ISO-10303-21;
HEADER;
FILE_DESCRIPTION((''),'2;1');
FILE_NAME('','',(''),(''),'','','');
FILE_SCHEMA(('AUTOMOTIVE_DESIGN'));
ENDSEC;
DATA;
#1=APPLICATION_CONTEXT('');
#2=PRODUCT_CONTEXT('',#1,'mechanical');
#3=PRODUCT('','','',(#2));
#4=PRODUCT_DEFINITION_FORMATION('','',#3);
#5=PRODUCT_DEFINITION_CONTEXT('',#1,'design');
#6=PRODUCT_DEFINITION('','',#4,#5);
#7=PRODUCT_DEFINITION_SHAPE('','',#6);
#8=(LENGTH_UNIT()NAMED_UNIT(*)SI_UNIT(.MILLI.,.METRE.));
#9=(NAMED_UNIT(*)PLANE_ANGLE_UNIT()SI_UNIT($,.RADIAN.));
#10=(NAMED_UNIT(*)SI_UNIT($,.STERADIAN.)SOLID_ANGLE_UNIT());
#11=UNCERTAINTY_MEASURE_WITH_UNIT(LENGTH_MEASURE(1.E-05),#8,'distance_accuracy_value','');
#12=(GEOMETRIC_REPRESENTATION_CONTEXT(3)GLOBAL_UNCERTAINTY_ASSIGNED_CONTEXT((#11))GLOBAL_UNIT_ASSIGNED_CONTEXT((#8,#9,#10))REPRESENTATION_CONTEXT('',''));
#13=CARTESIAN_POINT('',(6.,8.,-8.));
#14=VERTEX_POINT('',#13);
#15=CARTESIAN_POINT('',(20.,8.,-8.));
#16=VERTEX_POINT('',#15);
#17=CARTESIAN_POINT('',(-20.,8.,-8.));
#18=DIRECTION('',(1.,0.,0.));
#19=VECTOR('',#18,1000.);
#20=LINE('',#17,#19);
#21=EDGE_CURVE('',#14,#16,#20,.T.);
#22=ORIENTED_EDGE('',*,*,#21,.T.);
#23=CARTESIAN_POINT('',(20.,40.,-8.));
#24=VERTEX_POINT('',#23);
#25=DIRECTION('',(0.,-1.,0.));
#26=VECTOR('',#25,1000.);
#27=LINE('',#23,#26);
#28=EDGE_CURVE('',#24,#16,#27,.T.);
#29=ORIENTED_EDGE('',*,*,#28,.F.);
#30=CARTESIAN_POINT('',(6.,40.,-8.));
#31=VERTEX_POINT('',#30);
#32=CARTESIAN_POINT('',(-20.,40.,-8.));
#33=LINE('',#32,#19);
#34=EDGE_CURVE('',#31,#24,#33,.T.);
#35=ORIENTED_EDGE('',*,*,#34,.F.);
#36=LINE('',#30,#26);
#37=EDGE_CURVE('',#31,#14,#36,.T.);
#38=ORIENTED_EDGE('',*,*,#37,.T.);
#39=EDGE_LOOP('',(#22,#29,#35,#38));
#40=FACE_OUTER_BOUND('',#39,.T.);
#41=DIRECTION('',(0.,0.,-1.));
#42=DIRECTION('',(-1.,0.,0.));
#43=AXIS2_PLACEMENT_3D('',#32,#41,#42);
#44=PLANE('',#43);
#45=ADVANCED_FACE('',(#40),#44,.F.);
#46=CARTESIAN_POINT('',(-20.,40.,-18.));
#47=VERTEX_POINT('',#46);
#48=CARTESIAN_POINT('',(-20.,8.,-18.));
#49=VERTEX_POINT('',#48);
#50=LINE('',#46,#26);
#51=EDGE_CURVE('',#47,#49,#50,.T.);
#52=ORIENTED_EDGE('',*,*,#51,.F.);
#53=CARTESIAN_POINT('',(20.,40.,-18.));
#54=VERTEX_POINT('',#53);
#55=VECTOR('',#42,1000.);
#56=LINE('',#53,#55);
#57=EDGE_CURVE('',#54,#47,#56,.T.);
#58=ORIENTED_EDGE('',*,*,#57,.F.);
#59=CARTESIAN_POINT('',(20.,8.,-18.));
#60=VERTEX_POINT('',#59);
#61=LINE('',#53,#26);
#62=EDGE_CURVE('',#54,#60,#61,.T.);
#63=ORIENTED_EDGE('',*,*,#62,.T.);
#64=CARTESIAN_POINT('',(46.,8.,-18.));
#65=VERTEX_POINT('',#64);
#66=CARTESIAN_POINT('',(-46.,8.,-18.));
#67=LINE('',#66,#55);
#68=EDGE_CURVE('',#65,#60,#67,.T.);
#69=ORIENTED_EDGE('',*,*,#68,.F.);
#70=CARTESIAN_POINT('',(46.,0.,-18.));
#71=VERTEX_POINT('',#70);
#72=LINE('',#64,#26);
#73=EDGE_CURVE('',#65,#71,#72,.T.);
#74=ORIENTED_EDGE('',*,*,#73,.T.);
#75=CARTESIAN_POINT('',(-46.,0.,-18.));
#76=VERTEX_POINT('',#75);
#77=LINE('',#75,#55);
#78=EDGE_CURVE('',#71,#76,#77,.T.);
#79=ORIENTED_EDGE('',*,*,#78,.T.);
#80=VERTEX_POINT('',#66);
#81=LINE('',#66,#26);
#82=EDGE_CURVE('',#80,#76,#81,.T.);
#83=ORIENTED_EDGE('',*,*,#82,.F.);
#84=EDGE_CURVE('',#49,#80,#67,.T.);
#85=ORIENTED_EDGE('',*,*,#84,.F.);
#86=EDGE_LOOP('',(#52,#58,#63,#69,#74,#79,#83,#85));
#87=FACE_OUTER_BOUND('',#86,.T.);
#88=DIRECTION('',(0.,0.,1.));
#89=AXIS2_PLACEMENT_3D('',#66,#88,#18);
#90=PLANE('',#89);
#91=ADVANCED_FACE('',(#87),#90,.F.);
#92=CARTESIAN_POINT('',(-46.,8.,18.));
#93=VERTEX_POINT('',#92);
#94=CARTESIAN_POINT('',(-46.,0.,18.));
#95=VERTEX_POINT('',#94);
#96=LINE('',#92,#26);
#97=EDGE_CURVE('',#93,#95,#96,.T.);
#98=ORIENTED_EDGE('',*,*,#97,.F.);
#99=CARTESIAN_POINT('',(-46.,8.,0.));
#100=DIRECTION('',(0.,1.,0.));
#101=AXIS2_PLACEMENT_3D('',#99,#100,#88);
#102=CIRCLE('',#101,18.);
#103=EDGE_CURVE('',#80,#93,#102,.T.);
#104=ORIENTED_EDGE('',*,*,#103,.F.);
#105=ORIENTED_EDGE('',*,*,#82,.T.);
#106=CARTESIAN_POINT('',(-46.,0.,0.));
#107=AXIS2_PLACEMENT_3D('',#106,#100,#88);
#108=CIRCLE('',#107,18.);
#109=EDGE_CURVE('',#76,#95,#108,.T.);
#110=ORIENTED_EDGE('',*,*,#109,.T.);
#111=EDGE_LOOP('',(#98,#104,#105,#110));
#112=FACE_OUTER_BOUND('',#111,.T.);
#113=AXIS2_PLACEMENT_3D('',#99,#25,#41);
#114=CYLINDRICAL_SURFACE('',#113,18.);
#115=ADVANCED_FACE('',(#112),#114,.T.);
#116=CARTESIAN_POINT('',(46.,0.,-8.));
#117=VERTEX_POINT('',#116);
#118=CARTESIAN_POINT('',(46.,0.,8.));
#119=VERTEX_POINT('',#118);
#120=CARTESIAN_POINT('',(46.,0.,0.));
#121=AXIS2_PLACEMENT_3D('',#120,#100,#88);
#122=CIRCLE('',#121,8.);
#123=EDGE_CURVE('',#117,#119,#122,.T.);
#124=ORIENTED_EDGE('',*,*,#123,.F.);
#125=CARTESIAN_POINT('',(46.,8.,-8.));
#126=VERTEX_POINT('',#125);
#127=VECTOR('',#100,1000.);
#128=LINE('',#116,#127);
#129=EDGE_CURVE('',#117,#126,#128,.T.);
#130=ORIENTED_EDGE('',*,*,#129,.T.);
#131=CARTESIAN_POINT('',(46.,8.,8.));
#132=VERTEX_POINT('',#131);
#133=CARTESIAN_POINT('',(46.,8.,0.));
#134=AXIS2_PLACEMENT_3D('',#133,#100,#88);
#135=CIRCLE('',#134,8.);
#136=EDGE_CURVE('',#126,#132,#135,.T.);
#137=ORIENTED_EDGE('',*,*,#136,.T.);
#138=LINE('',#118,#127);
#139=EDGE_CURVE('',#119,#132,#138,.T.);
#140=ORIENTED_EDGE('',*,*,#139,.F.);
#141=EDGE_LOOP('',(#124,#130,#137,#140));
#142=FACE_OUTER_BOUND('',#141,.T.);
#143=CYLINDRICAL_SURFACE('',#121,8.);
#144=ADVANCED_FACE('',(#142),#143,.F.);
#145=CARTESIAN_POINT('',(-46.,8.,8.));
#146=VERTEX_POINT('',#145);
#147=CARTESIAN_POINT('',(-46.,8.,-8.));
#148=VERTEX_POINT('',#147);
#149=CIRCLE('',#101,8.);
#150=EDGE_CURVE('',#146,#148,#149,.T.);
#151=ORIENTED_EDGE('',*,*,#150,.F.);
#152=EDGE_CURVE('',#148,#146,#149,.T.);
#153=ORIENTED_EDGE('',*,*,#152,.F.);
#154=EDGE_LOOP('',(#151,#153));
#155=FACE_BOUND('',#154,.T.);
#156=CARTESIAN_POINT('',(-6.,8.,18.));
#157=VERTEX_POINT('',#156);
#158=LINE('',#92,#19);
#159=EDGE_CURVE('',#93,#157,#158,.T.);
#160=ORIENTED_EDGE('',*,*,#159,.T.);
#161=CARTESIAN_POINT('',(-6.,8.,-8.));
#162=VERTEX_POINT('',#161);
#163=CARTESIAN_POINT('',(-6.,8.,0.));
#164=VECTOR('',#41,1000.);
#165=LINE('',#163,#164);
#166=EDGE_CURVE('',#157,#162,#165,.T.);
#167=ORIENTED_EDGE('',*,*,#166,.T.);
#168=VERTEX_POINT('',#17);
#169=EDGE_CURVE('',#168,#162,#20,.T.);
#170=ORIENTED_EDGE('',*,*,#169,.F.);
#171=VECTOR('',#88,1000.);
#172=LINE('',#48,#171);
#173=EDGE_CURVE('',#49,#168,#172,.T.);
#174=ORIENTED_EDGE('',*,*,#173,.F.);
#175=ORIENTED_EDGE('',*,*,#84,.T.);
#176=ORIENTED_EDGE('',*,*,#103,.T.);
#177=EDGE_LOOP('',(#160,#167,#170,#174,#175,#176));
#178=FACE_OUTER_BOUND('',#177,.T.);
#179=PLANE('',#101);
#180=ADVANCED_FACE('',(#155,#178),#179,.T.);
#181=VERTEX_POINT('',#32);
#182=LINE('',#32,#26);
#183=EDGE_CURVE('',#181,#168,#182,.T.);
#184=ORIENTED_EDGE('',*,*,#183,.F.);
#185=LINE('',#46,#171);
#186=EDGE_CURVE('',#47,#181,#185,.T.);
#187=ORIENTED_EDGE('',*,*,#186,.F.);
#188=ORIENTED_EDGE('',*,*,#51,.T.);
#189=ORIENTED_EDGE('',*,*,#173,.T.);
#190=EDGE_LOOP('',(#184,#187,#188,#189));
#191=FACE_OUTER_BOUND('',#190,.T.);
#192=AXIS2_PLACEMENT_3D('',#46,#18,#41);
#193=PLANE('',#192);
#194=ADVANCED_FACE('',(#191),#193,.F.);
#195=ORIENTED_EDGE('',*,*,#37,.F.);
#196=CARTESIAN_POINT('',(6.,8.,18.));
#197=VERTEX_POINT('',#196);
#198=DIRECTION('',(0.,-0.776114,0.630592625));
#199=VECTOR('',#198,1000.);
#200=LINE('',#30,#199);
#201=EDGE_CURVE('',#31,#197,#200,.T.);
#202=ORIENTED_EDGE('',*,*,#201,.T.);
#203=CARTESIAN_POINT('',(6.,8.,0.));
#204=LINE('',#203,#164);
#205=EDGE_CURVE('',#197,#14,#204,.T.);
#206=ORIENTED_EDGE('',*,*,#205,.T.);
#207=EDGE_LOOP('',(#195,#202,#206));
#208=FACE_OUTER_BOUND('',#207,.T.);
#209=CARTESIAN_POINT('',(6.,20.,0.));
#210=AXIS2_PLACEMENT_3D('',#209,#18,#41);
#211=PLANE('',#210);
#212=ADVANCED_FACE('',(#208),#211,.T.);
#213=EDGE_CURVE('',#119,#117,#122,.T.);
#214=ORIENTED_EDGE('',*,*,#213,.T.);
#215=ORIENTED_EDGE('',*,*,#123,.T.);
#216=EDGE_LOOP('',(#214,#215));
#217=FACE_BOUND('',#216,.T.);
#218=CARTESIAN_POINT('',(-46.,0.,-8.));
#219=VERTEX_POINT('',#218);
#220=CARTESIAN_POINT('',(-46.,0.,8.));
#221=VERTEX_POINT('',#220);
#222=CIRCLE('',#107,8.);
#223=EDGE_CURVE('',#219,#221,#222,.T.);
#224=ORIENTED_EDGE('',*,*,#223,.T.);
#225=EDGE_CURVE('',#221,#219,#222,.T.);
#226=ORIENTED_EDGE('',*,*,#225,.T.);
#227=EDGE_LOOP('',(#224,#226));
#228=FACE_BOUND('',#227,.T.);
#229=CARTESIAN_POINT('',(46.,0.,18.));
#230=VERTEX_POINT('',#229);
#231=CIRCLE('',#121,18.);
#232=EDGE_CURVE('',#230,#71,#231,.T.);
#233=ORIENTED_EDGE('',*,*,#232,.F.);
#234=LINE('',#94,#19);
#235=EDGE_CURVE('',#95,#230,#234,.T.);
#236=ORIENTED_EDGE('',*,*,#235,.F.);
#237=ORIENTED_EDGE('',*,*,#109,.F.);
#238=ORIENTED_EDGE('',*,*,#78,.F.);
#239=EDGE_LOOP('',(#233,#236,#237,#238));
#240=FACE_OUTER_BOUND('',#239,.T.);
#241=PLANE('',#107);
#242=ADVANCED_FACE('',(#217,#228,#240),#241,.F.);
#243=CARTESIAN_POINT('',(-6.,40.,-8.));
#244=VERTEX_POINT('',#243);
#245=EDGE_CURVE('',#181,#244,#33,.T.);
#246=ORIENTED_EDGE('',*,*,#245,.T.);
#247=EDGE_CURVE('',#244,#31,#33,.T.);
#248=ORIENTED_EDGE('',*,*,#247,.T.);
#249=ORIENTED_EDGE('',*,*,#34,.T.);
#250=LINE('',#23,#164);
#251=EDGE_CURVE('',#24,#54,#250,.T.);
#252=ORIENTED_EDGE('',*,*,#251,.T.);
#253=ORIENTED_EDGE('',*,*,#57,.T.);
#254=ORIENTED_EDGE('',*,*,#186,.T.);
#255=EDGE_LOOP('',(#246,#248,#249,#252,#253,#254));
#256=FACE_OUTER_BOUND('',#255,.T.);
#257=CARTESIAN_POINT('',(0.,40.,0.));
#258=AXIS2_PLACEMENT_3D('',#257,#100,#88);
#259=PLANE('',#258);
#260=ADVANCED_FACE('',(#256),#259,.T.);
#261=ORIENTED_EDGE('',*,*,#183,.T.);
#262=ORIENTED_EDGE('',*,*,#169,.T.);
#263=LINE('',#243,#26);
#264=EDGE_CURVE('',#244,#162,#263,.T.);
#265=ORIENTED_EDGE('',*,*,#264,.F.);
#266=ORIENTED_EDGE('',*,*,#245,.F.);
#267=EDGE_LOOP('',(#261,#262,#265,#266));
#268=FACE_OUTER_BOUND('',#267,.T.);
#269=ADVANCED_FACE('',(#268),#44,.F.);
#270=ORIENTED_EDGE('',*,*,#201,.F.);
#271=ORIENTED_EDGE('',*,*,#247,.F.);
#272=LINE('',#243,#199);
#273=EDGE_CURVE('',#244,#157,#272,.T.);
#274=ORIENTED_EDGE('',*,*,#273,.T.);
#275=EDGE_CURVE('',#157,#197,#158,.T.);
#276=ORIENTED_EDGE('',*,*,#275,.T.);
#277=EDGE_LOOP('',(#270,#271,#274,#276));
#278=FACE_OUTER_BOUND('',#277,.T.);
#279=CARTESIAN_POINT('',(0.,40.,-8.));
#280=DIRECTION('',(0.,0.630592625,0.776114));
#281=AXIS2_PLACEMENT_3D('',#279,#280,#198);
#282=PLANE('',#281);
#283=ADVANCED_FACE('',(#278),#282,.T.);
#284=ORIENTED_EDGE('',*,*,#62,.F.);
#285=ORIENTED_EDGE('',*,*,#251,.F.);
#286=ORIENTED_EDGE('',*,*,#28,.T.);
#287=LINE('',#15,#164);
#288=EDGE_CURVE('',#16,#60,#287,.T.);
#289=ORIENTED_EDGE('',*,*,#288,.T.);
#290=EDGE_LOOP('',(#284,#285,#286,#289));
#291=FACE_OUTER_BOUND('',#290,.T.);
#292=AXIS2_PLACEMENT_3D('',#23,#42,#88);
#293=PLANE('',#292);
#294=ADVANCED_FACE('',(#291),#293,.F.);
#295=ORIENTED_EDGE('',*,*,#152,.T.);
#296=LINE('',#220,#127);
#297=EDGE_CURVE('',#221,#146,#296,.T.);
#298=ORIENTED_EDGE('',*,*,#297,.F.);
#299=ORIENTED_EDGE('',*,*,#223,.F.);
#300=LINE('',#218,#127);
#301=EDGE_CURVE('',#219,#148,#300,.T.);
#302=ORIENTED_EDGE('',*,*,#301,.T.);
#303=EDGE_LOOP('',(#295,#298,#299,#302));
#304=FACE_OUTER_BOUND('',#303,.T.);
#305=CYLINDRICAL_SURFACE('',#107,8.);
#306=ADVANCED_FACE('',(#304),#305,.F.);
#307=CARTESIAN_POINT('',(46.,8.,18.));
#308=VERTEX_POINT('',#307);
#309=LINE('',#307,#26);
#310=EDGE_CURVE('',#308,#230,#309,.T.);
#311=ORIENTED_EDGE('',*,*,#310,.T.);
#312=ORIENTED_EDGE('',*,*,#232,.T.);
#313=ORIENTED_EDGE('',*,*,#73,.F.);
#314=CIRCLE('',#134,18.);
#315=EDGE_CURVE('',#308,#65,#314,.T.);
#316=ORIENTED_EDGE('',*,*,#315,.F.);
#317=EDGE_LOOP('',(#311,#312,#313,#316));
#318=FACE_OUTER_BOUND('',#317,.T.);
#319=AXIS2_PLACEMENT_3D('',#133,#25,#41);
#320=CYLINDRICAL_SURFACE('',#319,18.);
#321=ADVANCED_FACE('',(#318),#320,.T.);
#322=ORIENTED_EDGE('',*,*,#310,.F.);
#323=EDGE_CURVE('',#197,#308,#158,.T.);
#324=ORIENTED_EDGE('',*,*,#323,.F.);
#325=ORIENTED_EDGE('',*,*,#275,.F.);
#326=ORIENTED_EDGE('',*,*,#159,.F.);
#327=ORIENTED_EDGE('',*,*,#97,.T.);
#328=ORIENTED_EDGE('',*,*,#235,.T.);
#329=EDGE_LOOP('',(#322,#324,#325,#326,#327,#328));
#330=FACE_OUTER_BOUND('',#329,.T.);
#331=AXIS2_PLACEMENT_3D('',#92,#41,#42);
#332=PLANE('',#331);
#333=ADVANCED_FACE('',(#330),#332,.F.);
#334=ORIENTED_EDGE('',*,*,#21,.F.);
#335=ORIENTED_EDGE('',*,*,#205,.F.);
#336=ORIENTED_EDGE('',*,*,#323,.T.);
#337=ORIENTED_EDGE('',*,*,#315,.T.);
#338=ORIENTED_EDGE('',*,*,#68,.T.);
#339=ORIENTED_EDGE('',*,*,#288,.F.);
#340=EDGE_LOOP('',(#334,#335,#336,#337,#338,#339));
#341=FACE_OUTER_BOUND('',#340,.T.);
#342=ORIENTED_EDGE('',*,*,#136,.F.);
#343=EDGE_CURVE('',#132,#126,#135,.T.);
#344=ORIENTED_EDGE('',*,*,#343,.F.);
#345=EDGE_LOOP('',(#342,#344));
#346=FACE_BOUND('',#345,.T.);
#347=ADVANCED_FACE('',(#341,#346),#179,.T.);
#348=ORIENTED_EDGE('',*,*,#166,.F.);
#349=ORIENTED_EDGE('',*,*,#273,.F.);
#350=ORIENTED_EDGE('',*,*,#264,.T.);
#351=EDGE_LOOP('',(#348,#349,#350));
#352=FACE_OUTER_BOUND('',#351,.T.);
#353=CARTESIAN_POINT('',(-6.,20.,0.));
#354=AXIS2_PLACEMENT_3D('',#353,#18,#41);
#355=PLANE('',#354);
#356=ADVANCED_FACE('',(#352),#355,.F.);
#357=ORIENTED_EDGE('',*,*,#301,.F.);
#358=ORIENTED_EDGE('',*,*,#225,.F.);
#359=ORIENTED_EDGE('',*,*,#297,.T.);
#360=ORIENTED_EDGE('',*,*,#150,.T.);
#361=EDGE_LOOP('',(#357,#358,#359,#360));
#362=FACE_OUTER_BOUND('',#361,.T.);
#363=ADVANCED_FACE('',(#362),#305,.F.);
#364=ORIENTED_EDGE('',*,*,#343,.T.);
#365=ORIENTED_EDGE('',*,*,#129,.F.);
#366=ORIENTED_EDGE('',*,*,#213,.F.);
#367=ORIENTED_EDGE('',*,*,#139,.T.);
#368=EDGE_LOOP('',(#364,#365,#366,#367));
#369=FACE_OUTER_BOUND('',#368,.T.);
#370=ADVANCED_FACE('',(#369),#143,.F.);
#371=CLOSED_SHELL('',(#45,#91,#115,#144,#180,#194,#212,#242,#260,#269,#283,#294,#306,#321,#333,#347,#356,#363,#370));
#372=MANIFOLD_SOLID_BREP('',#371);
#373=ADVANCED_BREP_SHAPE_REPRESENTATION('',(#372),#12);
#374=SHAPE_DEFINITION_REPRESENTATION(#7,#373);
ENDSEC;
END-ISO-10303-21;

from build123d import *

# Parameters (mm, degrees)
BASE_PLATE_DEPTH          = 8
MOUNTING_HOLES_SKETCH_R   = 8
MOUNTING_HOLES_2X_DEPTH   = 8
UPRIGHT_DEPTH             = 32
SUPPORT_RIB_REACH         = 79.589
SUPPORT_RIB_SKETCH_WALL_W = 198.408374186
SUPPORT_RIB_SKETCH_WALL_H = 12


with BuildPart() as part:
    # Base Plate Sketch → Base Plate (new body)
    with BuildSketch(Plane(origin=(0, 0, 0), x_dir=(1, 0, 0), z_dir=(0, 1, 0))):
        with BuildLine():
            Line((-46, 18), (46, 18))
            ThreePointArc((46, 18), (64, 0), (46, -18))
            Line((46, -18), (-46, -18))
            ThreePointArc((-46, -18), (-64, 0), (-46, 18))
        make_face()
    extrude(amount=BASE_PLATE_DEPTH)

    # Mounting Holes Sketch → Mounting Holes 2x (cut)
    with BuildSketch(Plane(origin=(0, 8, 0), x_dir=(1, 0, 0), z_dir=(0, 1, 0))):
        with Locations(Location((-46, 0, 0), (0, 0, 270))):
            Circle(MOUNTING_HOLES_SKETCH_R)
        with Locations(Location((46, 0, 0), (0, 0, 270))):
            Circle(MOUNTING_HOLES_SKETCH_R)
    extrude(amount=-MOUNTING_HOLES_2X_DEPTH, mode=Mode.SUBTRACT)

    # Upright Sketch → Upright (add)
    with BuildSketch(Plane(origin=(0, 8, 0), x_dir=(1, 0, 0), z_dir=(0, 1, 0))):
        Polygon((0, 18), (-20, 18), (-20, 8), (20, 8), (20, 18), align=None)
    extrude(amount=UPRIGHT_DEPTH)

    # Support Rib Sketch wall → Support Rib (add, up to next)
    with BuildSketch(Plane(origin=(0, 24, 5), x_dir=(0, -0.776114000116, 0.630592625094), z_dir=(0, -0.630592625094, -0.776114000116)), mode=Mode.PRIVATE) as support_rib_sk1:
        Rectangle(SUPPORT_RIB_SKETCH_WALL_W, SUPPORT_RIB_SKETCH_WALL_H)
    support_rib_tool1 = extrude(support_rib_sk1.sketch, amount=SUPPORT_RIB_REACH, mode=Mode.PRIVATE) - part.part
    add(support_rib_tool1.solids().sort_by_distance((0, 24, 5))[0])


solid = part.part
